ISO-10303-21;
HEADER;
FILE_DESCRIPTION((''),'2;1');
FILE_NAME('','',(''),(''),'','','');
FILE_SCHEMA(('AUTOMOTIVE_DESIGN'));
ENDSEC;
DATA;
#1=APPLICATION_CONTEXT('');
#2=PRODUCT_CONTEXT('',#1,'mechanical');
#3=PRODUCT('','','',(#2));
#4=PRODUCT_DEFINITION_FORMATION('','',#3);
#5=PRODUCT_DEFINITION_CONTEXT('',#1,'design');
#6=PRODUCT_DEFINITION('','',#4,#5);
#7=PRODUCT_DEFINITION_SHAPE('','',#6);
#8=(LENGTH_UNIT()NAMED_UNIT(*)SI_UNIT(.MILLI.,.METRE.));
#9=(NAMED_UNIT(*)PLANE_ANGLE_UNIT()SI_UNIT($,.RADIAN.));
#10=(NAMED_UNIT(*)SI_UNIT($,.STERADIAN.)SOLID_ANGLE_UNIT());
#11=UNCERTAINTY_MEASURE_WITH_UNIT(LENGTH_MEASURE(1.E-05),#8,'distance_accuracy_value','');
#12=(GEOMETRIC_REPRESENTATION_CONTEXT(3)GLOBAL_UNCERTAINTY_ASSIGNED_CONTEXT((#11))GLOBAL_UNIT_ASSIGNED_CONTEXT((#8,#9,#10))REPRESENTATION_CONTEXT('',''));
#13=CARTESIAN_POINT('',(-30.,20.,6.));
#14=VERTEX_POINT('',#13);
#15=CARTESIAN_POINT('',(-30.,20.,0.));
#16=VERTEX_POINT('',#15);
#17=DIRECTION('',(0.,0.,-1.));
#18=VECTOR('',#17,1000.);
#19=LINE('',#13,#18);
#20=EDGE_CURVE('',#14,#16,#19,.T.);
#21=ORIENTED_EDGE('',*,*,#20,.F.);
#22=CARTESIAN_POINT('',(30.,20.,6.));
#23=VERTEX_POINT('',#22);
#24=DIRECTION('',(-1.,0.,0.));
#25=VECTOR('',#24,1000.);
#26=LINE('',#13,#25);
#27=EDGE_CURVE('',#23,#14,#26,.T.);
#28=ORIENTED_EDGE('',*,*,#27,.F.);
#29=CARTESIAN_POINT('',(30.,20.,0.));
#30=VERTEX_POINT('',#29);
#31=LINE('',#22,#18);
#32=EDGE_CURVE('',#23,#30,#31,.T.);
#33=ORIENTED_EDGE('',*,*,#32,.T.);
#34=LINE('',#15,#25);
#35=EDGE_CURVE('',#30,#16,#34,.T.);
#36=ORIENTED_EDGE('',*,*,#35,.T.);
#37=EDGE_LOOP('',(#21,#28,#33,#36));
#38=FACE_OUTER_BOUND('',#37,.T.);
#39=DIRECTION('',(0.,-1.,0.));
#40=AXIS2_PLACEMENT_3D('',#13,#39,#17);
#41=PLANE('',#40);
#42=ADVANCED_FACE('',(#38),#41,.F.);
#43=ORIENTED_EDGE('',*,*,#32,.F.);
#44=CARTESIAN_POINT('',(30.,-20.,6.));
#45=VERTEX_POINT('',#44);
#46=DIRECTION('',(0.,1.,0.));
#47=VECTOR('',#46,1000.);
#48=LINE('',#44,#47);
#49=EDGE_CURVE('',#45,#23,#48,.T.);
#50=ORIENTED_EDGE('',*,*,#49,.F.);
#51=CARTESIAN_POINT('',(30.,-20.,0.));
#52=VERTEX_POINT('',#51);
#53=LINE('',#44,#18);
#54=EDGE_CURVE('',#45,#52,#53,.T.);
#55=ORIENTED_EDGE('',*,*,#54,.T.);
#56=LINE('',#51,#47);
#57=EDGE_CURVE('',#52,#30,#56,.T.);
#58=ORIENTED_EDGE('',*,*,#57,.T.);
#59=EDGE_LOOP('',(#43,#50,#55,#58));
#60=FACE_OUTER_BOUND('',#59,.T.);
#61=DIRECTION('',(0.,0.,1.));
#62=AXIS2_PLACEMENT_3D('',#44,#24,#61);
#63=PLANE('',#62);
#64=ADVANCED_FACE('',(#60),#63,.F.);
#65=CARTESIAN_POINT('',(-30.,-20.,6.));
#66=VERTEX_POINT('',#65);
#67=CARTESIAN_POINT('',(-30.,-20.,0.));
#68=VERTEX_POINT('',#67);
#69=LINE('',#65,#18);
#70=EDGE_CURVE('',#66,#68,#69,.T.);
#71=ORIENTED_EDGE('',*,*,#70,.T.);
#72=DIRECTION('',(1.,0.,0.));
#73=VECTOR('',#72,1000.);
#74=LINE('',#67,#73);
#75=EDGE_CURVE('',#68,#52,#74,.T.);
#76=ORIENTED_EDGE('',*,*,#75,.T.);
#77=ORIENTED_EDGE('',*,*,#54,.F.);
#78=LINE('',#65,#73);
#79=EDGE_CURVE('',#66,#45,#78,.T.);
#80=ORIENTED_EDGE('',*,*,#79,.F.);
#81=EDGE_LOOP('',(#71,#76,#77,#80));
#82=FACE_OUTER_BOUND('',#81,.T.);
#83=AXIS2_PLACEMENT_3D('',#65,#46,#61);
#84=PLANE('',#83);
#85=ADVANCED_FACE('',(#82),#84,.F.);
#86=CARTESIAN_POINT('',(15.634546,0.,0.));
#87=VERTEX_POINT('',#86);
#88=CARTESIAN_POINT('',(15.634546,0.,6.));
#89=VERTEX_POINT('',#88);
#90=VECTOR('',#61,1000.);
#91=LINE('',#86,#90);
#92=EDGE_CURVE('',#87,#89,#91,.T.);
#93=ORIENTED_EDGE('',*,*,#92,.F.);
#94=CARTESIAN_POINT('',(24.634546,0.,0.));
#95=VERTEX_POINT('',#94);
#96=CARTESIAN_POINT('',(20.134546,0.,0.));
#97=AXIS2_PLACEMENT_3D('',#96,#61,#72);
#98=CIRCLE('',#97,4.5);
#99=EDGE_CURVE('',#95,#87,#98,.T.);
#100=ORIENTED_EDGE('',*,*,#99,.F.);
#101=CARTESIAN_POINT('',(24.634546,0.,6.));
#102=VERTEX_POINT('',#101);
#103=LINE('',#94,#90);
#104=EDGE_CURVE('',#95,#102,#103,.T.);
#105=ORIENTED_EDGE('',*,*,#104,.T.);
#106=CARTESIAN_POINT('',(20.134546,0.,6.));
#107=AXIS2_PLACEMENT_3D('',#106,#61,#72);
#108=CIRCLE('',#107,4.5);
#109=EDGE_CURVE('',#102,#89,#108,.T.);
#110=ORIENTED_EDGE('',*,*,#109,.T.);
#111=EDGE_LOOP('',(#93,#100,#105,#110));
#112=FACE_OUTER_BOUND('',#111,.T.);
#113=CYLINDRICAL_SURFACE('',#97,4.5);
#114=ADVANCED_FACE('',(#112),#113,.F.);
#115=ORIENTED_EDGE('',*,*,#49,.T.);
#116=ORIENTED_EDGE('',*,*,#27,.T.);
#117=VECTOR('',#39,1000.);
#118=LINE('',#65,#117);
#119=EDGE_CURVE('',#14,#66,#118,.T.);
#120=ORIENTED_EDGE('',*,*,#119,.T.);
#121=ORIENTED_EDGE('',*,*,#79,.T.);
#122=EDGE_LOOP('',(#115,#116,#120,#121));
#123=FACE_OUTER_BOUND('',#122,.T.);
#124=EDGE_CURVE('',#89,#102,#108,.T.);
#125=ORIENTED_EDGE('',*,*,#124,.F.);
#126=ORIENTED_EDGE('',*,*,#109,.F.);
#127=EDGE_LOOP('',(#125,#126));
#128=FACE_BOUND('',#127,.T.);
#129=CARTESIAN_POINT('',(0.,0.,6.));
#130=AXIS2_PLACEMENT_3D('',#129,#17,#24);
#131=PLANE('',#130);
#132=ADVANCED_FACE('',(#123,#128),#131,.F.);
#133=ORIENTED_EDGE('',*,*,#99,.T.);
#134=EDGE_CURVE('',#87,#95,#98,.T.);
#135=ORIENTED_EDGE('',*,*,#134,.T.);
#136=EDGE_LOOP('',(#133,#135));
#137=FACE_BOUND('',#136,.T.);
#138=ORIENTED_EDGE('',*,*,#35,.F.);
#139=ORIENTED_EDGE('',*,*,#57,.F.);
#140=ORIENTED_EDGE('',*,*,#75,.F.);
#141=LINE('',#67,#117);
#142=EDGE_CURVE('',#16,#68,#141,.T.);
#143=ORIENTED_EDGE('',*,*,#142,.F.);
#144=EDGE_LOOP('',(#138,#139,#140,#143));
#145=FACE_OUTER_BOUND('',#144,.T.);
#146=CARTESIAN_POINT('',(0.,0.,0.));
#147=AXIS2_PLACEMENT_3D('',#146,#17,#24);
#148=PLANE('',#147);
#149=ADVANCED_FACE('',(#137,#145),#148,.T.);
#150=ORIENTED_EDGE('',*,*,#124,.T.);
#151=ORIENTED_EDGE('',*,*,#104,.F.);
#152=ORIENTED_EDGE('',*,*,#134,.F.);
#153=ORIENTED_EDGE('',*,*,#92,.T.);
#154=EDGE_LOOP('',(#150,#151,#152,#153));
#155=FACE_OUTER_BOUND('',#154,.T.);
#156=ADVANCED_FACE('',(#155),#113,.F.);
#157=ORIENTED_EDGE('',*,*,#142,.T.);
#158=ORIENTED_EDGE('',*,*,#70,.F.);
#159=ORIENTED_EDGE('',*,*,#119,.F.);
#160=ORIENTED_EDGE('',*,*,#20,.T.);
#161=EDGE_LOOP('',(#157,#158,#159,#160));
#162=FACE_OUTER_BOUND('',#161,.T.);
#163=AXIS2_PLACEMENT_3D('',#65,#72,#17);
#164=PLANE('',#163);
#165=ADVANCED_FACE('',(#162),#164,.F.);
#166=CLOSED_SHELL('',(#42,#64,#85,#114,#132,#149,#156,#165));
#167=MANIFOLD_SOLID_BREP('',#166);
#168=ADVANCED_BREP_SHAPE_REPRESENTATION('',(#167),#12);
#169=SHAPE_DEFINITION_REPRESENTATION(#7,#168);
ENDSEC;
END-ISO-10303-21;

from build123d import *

# Parameters (mm, degrees)
SKETCH1_W           = 60
SKETCH1_H           = 40
BOSS_EXTRUDE1_DEPTH = 6
SKETCH2_R           = 4.5
CUT_EXTRUDE1_DEPTH  = 6


with BuildPart() as part:
    # Sketch1 → Boss-Extrude1 (new body)
    with BuildSketch(Plane.XY):
        Rectangle(SKETCH1_W, SKETCH1_H)
    extrude(amount=BOSS_EXTRUDE1_DEPTH)

    # Sketch2 → Cut-Extrude1 (cut)
    with BuildSketch(Plane.XY.offset(6)):
        with Locations((20.134545778, 0)):
            Circle(SKETCH2_R)
    extrude(amount=-CUT_EXTRUDE1_DEPTH, mode=Mode.SUBTRACT)


solid = part.part
